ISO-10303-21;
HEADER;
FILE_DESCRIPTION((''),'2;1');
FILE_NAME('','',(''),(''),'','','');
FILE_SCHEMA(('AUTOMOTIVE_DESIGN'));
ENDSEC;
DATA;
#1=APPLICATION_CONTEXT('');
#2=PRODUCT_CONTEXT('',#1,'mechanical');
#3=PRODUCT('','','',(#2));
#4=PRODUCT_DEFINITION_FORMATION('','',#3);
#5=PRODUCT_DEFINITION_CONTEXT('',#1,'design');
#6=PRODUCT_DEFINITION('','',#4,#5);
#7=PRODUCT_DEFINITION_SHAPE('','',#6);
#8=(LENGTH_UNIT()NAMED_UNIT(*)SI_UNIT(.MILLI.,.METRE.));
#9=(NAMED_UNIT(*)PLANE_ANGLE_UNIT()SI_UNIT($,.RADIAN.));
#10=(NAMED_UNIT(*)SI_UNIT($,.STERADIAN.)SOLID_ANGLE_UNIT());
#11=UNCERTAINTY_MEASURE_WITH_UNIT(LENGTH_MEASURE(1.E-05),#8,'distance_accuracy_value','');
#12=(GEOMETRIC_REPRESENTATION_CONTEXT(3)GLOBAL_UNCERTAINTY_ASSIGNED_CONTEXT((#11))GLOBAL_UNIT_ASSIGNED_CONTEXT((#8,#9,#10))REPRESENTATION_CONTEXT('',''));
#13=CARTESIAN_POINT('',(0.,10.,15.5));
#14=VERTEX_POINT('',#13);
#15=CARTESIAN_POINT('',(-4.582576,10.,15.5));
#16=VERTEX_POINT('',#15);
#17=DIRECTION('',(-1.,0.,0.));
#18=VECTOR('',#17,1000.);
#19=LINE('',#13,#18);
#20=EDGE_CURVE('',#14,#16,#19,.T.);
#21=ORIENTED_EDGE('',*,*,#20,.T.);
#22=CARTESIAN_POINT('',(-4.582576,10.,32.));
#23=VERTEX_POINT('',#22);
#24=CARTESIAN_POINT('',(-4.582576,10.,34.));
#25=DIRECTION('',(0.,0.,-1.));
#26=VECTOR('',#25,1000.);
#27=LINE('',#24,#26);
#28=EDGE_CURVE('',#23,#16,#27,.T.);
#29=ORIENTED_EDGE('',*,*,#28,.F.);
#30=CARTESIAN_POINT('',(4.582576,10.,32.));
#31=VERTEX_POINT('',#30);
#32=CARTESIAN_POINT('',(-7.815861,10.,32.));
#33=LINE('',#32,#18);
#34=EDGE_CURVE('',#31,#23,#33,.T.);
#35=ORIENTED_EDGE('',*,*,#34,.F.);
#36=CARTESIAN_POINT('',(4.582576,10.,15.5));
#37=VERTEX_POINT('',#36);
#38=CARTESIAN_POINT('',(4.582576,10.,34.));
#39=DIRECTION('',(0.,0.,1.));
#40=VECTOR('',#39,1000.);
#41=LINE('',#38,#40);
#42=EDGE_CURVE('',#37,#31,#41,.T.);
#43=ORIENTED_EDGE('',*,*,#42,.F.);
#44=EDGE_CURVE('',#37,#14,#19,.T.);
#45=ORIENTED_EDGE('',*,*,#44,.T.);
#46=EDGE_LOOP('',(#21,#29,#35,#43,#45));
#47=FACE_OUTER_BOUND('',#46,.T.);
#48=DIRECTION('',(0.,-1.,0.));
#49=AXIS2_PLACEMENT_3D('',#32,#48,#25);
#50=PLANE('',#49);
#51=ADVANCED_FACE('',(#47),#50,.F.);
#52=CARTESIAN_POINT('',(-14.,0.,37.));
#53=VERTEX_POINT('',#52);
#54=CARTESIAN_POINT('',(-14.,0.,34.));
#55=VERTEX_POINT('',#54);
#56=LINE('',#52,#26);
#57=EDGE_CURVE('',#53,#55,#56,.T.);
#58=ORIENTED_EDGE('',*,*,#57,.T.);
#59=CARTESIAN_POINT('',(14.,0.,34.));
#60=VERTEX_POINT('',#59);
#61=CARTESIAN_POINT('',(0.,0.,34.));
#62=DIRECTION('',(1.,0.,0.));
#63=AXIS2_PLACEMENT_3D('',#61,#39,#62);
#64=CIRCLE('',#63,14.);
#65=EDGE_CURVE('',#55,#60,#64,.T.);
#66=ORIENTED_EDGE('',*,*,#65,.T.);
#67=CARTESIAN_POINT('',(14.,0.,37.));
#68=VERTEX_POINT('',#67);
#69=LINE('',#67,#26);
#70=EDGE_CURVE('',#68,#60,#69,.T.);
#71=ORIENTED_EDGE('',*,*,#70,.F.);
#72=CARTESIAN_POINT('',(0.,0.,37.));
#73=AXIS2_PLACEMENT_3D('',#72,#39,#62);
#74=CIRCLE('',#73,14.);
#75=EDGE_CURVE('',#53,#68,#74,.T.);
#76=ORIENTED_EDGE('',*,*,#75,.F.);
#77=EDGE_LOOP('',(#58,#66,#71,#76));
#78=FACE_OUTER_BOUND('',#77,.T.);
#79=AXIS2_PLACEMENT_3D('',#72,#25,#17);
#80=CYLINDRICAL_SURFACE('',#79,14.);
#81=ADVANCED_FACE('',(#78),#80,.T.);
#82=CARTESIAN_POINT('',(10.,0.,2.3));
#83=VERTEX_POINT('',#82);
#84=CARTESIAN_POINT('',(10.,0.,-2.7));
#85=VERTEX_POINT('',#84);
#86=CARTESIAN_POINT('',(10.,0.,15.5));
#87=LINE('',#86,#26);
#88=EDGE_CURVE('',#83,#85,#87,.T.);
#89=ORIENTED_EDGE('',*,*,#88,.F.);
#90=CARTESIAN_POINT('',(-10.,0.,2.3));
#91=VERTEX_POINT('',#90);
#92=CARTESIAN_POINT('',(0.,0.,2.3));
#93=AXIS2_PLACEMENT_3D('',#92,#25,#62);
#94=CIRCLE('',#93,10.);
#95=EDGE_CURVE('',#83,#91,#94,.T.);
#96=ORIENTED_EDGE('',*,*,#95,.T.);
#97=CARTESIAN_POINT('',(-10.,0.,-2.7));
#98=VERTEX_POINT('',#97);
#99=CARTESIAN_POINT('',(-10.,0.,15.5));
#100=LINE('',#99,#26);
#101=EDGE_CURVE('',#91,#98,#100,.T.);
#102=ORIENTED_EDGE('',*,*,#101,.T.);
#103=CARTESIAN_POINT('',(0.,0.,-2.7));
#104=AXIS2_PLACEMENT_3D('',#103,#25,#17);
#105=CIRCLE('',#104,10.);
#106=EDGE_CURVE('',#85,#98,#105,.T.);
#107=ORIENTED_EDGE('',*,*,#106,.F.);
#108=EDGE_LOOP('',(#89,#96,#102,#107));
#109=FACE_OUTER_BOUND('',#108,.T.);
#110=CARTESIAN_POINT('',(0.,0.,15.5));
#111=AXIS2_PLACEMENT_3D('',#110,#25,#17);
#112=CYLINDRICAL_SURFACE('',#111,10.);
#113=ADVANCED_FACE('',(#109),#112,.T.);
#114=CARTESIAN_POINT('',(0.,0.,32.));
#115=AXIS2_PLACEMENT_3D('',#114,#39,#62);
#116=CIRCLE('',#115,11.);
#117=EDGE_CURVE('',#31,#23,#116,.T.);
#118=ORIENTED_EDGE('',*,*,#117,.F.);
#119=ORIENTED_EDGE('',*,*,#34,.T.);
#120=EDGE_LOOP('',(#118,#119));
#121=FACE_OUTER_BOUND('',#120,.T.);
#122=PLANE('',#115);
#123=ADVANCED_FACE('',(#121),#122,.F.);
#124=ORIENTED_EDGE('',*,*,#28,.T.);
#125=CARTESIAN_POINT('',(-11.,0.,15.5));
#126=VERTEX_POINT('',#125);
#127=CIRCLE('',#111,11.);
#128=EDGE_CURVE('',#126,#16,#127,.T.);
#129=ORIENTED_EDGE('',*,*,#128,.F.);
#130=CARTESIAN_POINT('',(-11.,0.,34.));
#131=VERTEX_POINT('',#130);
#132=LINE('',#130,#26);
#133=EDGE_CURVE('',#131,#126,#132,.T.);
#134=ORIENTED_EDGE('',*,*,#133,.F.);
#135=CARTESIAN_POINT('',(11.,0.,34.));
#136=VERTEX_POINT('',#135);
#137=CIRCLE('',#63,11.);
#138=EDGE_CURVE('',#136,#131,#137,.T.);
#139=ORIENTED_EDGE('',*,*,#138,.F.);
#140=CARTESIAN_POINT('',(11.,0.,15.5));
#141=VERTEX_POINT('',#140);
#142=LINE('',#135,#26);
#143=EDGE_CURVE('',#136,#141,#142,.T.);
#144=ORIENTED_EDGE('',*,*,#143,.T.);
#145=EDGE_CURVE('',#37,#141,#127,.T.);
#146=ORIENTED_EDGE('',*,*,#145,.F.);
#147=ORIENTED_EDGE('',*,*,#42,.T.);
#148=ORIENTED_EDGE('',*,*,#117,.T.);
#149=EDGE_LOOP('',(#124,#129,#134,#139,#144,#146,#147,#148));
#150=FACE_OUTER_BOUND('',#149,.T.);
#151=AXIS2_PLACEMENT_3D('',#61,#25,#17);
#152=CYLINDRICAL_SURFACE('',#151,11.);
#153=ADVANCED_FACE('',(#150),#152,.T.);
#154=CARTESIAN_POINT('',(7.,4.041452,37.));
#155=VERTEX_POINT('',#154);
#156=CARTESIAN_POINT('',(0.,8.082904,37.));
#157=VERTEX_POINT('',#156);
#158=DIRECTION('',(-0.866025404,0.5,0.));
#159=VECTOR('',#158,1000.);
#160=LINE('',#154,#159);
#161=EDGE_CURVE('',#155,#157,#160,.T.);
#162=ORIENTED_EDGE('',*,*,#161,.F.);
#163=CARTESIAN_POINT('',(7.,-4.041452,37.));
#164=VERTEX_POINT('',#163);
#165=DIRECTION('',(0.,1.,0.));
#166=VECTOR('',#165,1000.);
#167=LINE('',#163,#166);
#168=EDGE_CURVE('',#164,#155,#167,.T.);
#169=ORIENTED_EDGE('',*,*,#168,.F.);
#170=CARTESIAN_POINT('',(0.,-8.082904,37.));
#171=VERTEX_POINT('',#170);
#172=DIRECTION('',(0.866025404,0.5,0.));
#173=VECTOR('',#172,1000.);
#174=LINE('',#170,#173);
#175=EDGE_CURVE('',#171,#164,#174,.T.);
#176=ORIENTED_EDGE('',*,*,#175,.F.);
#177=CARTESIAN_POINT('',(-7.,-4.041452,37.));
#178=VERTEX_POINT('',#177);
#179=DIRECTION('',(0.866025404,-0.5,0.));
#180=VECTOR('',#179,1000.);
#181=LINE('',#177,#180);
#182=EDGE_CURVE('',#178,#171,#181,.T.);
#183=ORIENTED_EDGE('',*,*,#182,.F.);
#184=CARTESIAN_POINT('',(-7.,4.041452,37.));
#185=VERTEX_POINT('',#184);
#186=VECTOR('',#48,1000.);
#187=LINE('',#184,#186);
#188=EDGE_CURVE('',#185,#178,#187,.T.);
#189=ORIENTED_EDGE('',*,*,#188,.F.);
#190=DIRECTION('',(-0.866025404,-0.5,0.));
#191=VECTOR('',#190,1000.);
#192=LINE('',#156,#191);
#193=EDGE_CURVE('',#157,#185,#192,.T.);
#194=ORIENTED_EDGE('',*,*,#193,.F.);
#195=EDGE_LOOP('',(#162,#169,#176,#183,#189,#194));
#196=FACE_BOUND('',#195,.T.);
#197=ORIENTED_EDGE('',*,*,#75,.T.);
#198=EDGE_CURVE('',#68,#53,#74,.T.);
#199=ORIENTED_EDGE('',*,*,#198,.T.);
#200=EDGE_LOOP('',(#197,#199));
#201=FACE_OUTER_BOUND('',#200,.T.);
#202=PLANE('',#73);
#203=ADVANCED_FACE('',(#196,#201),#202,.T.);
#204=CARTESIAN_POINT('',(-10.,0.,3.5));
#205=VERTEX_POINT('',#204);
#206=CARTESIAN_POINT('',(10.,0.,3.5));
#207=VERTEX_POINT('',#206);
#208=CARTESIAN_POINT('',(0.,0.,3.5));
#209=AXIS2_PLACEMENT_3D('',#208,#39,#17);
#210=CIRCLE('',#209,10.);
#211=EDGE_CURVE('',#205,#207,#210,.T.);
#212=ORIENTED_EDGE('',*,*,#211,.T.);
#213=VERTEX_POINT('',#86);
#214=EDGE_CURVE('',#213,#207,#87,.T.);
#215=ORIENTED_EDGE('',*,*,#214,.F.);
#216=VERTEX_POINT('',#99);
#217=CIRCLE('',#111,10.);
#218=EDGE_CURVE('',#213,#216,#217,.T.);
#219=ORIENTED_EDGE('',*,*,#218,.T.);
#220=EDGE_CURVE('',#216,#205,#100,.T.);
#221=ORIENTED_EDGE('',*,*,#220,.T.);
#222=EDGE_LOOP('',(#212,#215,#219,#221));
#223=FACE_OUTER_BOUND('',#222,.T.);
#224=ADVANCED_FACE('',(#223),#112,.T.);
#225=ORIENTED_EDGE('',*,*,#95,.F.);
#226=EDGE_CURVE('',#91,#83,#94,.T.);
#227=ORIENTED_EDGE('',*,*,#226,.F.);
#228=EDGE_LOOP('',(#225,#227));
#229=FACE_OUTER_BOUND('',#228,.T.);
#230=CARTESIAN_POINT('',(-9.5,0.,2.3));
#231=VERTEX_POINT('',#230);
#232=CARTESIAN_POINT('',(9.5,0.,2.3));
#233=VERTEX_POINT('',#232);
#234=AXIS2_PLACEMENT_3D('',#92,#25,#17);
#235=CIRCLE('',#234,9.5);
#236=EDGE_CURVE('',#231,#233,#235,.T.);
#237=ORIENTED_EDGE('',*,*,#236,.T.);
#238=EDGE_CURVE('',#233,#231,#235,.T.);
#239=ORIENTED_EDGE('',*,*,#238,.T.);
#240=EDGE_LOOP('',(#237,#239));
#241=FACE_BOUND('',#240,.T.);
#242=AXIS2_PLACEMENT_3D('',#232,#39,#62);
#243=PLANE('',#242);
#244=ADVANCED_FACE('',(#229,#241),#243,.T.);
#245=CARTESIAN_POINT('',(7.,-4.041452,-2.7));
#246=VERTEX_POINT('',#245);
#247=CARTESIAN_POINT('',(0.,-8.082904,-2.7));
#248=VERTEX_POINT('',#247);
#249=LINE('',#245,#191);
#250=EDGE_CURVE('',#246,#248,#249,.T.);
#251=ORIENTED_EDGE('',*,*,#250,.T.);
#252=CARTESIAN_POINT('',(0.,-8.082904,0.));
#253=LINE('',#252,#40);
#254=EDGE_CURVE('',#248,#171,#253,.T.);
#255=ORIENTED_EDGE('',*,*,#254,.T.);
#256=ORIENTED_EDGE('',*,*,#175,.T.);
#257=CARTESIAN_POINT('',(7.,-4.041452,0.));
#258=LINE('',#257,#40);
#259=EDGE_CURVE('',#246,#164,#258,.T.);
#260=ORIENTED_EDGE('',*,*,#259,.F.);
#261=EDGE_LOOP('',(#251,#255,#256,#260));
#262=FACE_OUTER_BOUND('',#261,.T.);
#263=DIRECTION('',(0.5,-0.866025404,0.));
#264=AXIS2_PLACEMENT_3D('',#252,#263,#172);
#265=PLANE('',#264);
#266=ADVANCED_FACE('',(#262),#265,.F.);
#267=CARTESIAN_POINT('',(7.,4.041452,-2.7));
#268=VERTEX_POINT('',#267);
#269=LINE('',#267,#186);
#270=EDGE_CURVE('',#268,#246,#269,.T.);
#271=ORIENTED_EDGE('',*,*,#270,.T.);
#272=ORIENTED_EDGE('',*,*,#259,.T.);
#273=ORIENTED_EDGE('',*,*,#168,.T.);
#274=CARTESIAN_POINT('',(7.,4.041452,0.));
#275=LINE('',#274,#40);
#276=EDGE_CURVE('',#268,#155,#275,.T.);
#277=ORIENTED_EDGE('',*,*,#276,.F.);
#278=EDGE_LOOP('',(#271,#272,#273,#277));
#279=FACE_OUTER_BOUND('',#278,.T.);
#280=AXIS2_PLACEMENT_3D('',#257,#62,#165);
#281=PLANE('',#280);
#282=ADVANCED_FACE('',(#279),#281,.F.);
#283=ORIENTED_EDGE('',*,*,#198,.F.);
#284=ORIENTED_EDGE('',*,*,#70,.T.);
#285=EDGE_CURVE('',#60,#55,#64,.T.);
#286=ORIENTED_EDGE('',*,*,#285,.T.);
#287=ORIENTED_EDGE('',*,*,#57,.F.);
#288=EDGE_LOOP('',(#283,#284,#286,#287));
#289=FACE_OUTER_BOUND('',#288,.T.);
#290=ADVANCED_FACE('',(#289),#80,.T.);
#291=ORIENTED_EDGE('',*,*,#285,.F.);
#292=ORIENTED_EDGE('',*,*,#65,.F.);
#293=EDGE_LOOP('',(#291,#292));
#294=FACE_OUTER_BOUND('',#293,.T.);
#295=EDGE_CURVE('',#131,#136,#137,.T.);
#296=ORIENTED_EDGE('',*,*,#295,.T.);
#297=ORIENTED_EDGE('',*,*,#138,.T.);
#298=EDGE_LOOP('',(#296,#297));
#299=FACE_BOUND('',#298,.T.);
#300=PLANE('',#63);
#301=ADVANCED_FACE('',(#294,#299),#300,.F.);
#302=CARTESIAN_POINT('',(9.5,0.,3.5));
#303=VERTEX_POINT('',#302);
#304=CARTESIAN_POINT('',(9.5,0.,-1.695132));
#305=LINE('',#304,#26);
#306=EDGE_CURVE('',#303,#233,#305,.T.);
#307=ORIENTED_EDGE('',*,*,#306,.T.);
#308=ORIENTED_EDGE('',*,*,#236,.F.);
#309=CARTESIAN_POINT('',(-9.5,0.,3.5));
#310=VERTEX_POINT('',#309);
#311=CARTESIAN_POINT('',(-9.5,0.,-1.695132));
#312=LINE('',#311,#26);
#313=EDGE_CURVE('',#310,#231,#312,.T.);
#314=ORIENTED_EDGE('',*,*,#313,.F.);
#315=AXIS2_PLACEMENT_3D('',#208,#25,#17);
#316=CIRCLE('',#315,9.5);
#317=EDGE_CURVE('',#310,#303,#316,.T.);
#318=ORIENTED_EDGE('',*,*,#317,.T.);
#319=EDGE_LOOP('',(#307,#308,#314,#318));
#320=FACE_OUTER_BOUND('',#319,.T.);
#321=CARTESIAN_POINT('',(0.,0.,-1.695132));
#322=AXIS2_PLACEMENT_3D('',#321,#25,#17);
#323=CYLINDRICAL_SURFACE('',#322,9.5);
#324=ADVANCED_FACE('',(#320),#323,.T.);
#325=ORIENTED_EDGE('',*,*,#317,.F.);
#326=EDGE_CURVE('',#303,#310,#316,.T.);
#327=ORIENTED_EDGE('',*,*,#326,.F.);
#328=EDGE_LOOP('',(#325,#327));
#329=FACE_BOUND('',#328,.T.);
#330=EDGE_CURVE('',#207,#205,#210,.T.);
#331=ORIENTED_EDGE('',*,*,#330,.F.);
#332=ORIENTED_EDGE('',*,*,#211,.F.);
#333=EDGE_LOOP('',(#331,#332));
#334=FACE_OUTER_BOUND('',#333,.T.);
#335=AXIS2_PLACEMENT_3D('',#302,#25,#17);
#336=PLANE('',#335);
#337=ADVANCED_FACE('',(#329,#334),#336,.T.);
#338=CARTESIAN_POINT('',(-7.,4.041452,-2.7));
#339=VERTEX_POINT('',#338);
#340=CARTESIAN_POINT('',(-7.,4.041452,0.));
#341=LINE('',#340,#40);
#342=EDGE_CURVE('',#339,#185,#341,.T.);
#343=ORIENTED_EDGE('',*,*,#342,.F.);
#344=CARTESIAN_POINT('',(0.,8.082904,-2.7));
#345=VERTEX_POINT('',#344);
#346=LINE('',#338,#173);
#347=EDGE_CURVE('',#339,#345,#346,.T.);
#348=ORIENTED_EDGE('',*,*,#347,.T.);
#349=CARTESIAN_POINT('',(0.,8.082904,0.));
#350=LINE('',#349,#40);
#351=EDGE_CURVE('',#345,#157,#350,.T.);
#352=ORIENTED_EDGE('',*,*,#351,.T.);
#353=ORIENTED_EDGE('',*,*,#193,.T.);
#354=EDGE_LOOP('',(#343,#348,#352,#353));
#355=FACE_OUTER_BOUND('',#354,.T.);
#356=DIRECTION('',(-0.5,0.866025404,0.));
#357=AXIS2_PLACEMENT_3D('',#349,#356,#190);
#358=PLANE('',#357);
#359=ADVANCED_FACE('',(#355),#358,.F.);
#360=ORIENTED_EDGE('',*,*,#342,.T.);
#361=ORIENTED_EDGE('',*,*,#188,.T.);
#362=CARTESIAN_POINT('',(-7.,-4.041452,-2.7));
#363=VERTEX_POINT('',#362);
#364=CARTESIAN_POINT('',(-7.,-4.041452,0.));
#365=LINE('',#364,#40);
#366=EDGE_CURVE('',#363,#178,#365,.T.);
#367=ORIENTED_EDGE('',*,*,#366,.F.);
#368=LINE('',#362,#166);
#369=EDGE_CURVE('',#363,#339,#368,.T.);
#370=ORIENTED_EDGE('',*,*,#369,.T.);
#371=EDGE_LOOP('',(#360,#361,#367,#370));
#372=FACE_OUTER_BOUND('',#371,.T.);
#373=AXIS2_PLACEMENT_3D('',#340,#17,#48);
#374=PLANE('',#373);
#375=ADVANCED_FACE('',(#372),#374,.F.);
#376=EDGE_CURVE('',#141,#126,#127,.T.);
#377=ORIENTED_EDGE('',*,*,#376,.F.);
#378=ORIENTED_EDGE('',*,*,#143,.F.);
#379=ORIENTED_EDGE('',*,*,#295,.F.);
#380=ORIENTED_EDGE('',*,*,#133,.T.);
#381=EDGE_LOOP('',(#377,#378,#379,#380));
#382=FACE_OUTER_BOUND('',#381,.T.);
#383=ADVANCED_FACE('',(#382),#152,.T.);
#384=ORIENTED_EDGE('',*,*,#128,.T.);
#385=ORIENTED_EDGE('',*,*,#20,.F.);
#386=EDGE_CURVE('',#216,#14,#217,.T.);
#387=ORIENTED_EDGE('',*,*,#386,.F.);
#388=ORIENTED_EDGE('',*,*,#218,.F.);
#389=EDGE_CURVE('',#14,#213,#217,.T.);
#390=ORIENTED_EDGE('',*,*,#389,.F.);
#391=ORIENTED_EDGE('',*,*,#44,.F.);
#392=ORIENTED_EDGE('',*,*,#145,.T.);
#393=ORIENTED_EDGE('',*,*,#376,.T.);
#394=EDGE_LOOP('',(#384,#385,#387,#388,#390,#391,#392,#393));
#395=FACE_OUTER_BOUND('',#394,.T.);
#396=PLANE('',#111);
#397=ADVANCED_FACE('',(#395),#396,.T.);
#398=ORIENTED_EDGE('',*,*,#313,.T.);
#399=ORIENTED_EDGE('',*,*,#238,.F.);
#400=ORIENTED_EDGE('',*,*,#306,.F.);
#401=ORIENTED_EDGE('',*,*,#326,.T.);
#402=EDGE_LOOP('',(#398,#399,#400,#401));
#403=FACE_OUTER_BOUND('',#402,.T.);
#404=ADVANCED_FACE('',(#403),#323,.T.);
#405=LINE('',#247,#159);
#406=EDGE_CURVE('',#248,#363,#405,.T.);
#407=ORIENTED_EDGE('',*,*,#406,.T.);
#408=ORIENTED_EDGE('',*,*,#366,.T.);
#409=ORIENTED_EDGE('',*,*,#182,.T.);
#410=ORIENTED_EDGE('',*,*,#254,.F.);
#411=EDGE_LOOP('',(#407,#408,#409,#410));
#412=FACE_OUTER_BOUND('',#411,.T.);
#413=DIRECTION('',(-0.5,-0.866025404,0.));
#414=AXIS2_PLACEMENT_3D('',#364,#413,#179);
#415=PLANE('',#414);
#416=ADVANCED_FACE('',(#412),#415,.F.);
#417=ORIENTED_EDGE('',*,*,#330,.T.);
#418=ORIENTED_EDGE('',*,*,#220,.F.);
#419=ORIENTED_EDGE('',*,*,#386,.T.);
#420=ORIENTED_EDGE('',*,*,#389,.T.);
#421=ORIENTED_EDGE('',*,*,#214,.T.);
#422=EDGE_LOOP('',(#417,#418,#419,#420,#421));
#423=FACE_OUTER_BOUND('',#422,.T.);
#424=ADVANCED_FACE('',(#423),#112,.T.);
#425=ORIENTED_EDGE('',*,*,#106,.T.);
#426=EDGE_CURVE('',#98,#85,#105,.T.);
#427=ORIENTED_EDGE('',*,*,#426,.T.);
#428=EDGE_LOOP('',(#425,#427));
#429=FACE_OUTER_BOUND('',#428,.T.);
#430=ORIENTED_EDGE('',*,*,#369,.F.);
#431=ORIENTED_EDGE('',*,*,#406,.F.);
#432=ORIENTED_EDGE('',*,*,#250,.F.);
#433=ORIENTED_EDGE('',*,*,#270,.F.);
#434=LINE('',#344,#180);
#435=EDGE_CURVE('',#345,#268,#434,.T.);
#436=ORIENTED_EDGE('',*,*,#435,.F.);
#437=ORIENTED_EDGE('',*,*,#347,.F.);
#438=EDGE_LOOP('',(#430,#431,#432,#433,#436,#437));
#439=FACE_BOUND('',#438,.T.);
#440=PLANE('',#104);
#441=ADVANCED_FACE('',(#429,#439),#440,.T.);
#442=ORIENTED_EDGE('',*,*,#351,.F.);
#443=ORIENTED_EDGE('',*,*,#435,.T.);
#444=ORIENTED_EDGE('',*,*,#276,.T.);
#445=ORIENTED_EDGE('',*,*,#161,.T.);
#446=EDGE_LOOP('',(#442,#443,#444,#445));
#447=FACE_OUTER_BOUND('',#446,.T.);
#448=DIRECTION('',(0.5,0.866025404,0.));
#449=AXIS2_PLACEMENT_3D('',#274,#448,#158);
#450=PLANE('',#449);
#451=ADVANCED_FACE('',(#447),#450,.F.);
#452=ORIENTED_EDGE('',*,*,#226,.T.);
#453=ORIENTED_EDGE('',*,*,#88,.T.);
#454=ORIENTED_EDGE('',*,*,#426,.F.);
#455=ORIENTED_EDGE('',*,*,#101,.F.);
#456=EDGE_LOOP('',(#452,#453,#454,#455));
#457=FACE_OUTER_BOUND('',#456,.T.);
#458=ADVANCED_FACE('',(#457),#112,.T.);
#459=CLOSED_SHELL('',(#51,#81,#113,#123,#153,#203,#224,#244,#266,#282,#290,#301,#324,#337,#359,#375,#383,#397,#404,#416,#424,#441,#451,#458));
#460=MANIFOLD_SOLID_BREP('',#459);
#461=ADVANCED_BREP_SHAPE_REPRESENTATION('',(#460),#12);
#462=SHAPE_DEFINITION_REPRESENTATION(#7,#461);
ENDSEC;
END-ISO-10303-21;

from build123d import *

# Parameters (mm, degrees)
SKETCH_1_R          = 11
SKETCH_1_R_2        = 6
EXTRUDE_1_DEPTH     = 34
SKETCH_2_R          = 14
SKETCH_2_R_2        = 7
EXTRUDE_2_DEPTH     = 3
SKETCH_3_R          = 12.01734277
SKETCH_3_R_2        = 10
CUT_EXTRUDE_1_DEPTH = 15.5
SKETCH_4_W          = 13.23621111
SKETCH_4_H          = 1.977552999
CUT_EXTRUDE_2_DEPTH = 32
CUT_EXTRUDE_3_DEPTH = 42.964270517
SKETCH_6_W          = 1
SKETCH_6_H          = 1.2
EXTRUDE_START       = 2.7
SKETCH_7_R          = 10
EXTRUDE_3_DEPTH     = 2.7


with BuildPart() as part:
    # 草图1 → 凸台-拉伸1 (new body)
    with BuildSketch(Plane.XY):
        Circle(SKETCH_1_R)
        Circle(SKETCH_1_R_2, mode=Mode.SUBTRACT)
    extrude(amount=EXTRUDE_1_DEPTH)

    # 草图2 → 凸台-拉伸2 (add)
    with BuildSketch(Plane.XY.offset(34)):
        Circle(SKETCH_2_R)
        Circle(SKETCH_2_R_2, mode=Mode.SUBTRACT)
    extrude(amount=EXTRUDE_2_DEPTH)

    # 草图3 → 切除-拉伸1 (cut)
    with BuildSketch(Plane(origin=(0, 0, 0), x_dir=(-1, 0, 0), z_dir=(0, 0, -1))):
        Circle(SKETCH_3_R)
        Circle(SKETCH_3_R_2, mode=Mode.SUBTRACT)
    extrude(amount=-CUT_EXTRUDE_1_DEPTH, mode=Mode.SUBTRACT)

    # 草图4 → 切除-拉伸2 (cut)
    with BuildSketch(Plane(origin=(0, 0, 0), x_dir=(-1, 0, 0), z_dir=(0, 0, -1))):
        with Locations((1.1977553, 10.9887765)):
            Rectangle(SKETCH_4_W, SKETCH_4_H)
    extrude(amount=-CUT_EXTRUDE_2_DEPTH, mode=Mode.SUBTRACT)

    # 草图5 → 切除-拉伸3 (cut, through all)
    with BuildSketch(Plane.XY.offset(37)):
        Polygon((7, -4.041451884), (7, 4.041451884), (0, 8.082903769), (-7, 4.041451884), (-7, -4.041451884), (0, -8.082903769), align=None)
    extrude(amount=-CUT_EXTRUDE_3_DEPTH, mode=Mode.SUBTRACT)

    # 草图6 → 切除-旋转1 (revolve, cut)
    with BuildSketch(Plane(origin=(0, 0, 0), x_dir=(1, 0, 0), z_dir=(0, 1, 0)), mode=Mode.PRIVATE) as cut_revolve_1_sk:
        with Locations((10, -2.9)):
            Rectangle(SKETCH_6_W, SKETCH_6_H)
    revolve(cut_revolve_1_sk.sketch.rotate(Axis((0, 0, -1.695132032), (0, 0, 1)), 180), axis=Axis((0, 0, -1.695132032), (0, 0, 1)), mode=Mode.SUBTRACT)

    # 草图7 → 凸台-拉伸3 (add)
    with BuildSketch(Plane(origin=(0, 0, 0), x_dir=(-1, 0, 0), z_dir=(0, 0, -1)).offset(EXTRUDE_START)):
        Circle(SKETCH_7_R)
        Polygon((7, -4.041451884), (7, 4.041451884), (0, 8.082903769), (-7, 4.041451884), (-7, -4.041451884), (0, -8.082903769), align=None, mode=Mode.SUBTRACT)
    extrude(amount=-EXTRUDE_3_DEPTH)


solid = part.part
